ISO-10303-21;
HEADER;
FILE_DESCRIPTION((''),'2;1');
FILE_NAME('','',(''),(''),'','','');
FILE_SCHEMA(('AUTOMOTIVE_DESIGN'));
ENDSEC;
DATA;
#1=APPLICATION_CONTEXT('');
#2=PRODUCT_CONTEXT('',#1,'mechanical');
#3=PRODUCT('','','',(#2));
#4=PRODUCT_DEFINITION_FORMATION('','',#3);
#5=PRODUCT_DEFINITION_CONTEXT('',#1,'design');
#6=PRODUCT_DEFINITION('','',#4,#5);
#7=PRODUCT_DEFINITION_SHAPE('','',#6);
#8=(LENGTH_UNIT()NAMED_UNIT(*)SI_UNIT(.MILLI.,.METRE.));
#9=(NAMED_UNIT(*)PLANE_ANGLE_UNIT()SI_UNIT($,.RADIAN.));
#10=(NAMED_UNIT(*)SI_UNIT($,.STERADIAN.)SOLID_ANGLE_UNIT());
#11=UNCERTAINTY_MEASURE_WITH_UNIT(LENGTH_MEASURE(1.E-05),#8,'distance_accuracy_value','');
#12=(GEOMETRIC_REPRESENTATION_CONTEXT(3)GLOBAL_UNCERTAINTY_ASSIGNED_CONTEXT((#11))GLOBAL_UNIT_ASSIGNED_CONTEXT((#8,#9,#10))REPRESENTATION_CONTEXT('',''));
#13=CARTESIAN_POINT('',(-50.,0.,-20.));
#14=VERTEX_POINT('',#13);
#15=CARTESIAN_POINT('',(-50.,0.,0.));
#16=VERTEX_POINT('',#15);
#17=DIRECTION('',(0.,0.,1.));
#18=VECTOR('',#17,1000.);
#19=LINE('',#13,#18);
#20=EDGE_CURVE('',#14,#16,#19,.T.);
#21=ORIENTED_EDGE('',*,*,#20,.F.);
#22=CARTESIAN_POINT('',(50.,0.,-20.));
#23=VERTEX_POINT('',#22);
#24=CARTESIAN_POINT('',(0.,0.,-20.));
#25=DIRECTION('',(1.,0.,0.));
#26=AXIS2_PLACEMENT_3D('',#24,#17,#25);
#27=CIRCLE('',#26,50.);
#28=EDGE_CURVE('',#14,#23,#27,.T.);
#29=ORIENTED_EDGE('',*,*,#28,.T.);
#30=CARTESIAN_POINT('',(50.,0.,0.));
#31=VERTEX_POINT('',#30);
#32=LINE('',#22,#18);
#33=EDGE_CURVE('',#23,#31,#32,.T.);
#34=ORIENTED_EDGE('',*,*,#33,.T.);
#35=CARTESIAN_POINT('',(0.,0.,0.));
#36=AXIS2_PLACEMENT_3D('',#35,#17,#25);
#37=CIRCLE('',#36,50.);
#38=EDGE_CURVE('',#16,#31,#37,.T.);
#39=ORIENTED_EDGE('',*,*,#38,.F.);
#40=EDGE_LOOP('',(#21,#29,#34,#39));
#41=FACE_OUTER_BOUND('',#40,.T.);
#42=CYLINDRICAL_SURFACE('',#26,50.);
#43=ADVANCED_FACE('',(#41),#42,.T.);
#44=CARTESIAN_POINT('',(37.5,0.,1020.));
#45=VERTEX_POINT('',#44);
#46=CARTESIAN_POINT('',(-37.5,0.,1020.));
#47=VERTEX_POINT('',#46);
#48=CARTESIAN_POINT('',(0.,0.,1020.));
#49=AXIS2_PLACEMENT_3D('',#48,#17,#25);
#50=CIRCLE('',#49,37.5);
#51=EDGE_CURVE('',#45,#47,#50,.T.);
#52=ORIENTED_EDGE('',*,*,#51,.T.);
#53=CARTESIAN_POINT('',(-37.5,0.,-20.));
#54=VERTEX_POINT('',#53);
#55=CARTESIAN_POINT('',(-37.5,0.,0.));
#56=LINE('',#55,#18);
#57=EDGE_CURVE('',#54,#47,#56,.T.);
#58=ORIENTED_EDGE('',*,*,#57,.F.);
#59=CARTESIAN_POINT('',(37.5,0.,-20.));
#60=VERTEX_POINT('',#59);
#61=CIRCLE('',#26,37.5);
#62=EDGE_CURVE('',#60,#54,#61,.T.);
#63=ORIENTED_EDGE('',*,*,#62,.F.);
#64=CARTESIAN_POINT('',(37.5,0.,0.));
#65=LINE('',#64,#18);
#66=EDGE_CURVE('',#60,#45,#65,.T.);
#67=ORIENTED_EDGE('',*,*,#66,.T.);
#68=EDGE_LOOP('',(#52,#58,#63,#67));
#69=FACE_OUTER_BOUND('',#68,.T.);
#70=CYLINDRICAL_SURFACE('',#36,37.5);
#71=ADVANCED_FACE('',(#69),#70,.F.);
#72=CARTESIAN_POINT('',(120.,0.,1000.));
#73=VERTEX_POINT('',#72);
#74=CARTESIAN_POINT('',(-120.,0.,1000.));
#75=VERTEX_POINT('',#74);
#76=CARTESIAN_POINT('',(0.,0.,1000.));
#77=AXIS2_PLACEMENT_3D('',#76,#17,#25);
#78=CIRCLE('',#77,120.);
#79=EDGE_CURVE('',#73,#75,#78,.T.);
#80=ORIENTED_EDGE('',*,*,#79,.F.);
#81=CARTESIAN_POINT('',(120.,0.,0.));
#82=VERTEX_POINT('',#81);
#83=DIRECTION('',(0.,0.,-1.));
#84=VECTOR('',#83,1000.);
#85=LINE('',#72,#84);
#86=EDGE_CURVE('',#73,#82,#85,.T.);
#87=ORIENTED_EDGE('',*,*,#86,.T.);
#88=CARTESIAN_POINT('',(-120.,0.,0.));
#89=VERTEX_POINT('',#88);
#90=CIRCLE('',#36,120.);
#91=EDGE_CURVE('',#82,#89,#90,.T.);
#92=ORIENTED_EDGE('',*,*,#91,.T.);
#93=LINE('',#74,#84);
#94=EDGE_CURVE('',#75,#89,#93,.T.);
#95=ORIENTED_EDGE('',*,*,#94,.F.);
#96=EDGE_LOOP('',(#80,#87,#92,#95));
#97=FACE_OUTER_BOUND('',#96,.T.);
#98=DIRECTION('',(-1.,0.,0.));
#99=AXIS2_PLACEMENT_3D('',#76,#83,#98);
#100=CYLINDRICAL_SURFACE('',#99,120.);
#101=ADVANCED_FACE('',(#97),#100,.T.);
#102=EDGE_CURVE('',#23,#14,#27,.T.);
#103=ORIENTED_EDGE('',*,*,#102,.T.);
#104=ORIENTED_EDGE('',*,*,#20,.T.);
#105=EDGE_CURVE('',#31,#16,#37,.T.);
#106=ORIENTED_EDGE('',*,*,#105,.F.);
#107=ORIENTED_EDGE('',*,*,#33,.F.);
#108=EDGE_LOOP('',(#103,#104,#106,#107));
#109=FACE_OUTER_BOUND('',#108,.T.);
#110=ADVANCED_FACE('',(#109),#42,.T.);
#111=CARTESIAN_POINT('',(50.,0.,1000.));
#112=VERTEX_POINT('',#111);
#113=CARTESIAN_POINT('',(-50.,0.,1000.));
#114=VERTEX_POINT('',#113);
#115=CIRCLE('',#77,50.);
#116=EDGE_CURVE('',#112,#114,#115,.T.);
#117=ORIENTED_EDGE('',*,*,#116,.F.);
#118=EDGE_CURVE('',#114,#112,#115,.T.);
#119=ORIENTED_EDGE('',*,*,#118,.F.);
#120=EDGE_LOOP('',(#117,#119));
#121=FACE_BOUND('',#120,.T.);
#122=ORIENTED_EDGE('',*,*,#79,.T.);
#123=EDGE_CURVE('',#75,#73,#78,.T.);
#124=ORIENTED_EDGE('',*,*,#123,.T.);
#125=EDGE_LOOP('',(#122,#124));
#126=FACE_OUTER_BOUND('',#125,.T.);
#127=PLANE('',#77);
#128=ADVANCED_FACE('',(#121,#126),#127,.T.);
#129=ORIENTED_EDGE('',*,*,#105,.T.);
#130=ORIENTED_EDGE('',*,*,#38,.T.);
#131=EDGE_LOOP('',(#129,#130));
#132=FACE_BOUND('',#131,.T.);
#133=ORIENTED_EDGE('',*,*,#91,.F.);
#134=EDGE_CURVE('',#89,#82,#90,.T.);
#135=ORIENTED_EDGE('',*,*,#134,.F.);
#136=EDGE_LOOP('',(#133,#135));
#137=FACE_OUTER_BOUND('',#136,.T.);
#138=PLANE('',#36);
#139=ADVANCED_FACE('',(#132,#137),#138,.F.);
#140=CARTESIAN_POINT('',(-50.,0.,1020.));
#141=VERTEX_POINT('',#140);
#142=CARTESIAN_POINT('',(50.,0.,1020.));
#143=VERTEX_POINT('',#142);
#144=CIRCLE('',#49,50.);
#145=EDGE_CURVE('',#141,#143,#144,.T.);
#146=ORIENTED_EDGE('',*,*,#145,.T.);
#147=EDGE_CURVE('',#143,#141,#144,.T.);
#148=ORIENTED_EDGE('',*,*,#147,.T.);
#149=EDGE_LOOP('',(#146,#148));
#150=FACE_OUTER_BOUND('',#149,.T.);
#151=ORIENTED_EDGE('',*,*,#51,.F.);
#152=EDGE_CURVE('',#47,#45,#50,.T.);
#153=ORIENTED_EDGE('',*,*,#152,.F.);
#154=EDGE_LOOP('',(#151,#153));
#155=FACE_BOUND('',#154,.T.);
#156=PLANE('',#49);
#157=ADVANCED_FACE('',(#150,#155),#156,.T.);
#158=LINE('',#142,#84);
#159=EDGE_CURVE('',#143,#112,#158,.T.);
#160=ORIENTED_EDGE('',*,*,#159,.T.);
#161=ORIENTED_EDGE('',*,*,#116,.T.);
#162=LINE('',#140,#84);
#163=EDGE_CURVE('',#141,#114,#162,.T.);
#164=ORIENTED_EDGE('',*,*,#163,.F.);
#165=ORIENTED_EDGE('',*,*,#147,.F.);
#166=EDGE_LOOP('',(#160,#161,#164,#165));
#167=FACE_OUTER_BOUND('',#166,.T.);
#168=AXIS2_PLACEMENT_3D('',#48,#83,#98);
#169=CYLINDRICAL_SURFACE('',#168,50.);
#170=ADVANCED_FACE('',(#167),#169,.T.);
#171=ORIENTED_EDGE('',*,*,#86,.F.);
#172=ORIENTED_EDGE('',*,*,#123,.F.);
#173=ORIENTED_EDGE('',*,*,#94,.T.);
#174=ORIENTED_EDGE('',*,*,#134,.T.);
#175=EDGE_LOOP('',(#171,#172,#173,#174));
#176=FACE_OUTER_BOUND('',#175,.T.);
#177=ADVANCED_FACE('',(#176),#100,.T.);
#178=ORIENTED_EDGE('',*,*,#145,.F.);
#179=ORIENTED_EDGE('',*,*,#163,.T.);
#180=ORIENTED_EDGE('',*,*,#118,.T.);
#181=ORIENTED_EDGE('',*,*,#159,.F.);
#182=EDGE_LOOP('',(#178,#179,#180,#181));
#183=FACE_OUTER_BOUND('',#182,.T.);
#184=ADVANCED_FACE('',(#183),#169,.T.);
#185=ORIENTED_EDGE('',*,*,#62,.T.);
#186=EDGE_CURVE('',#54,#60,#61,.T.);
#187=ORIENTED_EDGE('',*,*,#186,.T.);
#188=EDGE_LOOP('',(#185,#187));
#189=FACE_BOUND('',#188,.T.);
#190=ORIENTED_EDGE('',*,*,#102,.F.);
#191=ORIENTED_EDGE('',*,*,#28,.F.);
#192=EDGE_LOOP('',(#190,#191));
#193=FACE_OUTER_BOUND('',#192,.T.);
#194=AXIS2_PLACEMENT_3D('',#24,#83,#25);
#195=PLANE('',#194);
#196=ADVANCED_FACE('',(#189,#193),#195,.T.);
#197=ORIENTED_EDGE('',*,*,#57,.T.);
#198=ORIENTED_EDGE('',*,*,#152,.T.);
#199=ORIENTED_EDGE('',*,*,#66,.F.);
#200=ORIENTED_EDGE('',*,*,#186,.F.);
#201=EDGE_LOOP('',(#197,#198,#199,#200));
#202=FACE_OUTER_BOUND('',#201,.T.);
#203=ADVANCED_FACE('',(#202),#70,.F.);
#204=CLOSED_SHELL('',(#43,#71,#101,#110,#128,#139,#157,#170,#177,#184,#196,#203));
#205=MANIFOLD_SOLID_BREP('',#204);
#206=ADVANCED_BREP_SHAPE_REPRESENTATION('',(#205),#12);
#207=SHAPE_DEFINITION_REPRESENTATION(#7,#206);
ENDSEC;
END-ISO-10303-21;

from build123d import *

# Parameters (mm, degrees)
SKETCH_1_R          = 120
EXTRUDE_1_DEPTH     = 1000
SKETCH_2_R          = 37.5
CUT_EXTRUDE_1_DEPTH = 1000
EXTRUDE_START       = 20
SKETCH_3_R          = 50
SKETCH_3_R_2        = 37.5
EXTRUDE_2_DEPTH     = 20


with BuildPart() as part:
    # 草图1 → 凸台-拉伸1 (new body)
    with BuildSketch(Plane.XY):
        Circle(SKETCH_1_R)
    extrude(amount=EXTRUDE_1_DEPTH)

    # 草图2 → 切除-拉伸1 (cut)
    with BuildSketch(Plane.XY.offset(1000)):
        Circle(SKETCH_2_R)
    extrude(amount=-CUT_EXTRUDE_1_DEPTH, mode=Mode.SUBTRACT)

    # 草图3 → 凸台-拉伸2 (add)
    with BuildSketch(Plane.XY.offset(1000).offset(EXTRUDE_START)):
        Circle(SKETCH_3_R)
        Circle(SKETCH_3_R_2, mode=Mode.SUBTRACT)
    extrude_2 = extrude(amount=-EXTRUDE_2_DEPTH)

    # 镜向1: 凸台-拉伸2 across plane
    add(extrude_2.mirror(Plane.XY.offset(500)))


solid = part.part
